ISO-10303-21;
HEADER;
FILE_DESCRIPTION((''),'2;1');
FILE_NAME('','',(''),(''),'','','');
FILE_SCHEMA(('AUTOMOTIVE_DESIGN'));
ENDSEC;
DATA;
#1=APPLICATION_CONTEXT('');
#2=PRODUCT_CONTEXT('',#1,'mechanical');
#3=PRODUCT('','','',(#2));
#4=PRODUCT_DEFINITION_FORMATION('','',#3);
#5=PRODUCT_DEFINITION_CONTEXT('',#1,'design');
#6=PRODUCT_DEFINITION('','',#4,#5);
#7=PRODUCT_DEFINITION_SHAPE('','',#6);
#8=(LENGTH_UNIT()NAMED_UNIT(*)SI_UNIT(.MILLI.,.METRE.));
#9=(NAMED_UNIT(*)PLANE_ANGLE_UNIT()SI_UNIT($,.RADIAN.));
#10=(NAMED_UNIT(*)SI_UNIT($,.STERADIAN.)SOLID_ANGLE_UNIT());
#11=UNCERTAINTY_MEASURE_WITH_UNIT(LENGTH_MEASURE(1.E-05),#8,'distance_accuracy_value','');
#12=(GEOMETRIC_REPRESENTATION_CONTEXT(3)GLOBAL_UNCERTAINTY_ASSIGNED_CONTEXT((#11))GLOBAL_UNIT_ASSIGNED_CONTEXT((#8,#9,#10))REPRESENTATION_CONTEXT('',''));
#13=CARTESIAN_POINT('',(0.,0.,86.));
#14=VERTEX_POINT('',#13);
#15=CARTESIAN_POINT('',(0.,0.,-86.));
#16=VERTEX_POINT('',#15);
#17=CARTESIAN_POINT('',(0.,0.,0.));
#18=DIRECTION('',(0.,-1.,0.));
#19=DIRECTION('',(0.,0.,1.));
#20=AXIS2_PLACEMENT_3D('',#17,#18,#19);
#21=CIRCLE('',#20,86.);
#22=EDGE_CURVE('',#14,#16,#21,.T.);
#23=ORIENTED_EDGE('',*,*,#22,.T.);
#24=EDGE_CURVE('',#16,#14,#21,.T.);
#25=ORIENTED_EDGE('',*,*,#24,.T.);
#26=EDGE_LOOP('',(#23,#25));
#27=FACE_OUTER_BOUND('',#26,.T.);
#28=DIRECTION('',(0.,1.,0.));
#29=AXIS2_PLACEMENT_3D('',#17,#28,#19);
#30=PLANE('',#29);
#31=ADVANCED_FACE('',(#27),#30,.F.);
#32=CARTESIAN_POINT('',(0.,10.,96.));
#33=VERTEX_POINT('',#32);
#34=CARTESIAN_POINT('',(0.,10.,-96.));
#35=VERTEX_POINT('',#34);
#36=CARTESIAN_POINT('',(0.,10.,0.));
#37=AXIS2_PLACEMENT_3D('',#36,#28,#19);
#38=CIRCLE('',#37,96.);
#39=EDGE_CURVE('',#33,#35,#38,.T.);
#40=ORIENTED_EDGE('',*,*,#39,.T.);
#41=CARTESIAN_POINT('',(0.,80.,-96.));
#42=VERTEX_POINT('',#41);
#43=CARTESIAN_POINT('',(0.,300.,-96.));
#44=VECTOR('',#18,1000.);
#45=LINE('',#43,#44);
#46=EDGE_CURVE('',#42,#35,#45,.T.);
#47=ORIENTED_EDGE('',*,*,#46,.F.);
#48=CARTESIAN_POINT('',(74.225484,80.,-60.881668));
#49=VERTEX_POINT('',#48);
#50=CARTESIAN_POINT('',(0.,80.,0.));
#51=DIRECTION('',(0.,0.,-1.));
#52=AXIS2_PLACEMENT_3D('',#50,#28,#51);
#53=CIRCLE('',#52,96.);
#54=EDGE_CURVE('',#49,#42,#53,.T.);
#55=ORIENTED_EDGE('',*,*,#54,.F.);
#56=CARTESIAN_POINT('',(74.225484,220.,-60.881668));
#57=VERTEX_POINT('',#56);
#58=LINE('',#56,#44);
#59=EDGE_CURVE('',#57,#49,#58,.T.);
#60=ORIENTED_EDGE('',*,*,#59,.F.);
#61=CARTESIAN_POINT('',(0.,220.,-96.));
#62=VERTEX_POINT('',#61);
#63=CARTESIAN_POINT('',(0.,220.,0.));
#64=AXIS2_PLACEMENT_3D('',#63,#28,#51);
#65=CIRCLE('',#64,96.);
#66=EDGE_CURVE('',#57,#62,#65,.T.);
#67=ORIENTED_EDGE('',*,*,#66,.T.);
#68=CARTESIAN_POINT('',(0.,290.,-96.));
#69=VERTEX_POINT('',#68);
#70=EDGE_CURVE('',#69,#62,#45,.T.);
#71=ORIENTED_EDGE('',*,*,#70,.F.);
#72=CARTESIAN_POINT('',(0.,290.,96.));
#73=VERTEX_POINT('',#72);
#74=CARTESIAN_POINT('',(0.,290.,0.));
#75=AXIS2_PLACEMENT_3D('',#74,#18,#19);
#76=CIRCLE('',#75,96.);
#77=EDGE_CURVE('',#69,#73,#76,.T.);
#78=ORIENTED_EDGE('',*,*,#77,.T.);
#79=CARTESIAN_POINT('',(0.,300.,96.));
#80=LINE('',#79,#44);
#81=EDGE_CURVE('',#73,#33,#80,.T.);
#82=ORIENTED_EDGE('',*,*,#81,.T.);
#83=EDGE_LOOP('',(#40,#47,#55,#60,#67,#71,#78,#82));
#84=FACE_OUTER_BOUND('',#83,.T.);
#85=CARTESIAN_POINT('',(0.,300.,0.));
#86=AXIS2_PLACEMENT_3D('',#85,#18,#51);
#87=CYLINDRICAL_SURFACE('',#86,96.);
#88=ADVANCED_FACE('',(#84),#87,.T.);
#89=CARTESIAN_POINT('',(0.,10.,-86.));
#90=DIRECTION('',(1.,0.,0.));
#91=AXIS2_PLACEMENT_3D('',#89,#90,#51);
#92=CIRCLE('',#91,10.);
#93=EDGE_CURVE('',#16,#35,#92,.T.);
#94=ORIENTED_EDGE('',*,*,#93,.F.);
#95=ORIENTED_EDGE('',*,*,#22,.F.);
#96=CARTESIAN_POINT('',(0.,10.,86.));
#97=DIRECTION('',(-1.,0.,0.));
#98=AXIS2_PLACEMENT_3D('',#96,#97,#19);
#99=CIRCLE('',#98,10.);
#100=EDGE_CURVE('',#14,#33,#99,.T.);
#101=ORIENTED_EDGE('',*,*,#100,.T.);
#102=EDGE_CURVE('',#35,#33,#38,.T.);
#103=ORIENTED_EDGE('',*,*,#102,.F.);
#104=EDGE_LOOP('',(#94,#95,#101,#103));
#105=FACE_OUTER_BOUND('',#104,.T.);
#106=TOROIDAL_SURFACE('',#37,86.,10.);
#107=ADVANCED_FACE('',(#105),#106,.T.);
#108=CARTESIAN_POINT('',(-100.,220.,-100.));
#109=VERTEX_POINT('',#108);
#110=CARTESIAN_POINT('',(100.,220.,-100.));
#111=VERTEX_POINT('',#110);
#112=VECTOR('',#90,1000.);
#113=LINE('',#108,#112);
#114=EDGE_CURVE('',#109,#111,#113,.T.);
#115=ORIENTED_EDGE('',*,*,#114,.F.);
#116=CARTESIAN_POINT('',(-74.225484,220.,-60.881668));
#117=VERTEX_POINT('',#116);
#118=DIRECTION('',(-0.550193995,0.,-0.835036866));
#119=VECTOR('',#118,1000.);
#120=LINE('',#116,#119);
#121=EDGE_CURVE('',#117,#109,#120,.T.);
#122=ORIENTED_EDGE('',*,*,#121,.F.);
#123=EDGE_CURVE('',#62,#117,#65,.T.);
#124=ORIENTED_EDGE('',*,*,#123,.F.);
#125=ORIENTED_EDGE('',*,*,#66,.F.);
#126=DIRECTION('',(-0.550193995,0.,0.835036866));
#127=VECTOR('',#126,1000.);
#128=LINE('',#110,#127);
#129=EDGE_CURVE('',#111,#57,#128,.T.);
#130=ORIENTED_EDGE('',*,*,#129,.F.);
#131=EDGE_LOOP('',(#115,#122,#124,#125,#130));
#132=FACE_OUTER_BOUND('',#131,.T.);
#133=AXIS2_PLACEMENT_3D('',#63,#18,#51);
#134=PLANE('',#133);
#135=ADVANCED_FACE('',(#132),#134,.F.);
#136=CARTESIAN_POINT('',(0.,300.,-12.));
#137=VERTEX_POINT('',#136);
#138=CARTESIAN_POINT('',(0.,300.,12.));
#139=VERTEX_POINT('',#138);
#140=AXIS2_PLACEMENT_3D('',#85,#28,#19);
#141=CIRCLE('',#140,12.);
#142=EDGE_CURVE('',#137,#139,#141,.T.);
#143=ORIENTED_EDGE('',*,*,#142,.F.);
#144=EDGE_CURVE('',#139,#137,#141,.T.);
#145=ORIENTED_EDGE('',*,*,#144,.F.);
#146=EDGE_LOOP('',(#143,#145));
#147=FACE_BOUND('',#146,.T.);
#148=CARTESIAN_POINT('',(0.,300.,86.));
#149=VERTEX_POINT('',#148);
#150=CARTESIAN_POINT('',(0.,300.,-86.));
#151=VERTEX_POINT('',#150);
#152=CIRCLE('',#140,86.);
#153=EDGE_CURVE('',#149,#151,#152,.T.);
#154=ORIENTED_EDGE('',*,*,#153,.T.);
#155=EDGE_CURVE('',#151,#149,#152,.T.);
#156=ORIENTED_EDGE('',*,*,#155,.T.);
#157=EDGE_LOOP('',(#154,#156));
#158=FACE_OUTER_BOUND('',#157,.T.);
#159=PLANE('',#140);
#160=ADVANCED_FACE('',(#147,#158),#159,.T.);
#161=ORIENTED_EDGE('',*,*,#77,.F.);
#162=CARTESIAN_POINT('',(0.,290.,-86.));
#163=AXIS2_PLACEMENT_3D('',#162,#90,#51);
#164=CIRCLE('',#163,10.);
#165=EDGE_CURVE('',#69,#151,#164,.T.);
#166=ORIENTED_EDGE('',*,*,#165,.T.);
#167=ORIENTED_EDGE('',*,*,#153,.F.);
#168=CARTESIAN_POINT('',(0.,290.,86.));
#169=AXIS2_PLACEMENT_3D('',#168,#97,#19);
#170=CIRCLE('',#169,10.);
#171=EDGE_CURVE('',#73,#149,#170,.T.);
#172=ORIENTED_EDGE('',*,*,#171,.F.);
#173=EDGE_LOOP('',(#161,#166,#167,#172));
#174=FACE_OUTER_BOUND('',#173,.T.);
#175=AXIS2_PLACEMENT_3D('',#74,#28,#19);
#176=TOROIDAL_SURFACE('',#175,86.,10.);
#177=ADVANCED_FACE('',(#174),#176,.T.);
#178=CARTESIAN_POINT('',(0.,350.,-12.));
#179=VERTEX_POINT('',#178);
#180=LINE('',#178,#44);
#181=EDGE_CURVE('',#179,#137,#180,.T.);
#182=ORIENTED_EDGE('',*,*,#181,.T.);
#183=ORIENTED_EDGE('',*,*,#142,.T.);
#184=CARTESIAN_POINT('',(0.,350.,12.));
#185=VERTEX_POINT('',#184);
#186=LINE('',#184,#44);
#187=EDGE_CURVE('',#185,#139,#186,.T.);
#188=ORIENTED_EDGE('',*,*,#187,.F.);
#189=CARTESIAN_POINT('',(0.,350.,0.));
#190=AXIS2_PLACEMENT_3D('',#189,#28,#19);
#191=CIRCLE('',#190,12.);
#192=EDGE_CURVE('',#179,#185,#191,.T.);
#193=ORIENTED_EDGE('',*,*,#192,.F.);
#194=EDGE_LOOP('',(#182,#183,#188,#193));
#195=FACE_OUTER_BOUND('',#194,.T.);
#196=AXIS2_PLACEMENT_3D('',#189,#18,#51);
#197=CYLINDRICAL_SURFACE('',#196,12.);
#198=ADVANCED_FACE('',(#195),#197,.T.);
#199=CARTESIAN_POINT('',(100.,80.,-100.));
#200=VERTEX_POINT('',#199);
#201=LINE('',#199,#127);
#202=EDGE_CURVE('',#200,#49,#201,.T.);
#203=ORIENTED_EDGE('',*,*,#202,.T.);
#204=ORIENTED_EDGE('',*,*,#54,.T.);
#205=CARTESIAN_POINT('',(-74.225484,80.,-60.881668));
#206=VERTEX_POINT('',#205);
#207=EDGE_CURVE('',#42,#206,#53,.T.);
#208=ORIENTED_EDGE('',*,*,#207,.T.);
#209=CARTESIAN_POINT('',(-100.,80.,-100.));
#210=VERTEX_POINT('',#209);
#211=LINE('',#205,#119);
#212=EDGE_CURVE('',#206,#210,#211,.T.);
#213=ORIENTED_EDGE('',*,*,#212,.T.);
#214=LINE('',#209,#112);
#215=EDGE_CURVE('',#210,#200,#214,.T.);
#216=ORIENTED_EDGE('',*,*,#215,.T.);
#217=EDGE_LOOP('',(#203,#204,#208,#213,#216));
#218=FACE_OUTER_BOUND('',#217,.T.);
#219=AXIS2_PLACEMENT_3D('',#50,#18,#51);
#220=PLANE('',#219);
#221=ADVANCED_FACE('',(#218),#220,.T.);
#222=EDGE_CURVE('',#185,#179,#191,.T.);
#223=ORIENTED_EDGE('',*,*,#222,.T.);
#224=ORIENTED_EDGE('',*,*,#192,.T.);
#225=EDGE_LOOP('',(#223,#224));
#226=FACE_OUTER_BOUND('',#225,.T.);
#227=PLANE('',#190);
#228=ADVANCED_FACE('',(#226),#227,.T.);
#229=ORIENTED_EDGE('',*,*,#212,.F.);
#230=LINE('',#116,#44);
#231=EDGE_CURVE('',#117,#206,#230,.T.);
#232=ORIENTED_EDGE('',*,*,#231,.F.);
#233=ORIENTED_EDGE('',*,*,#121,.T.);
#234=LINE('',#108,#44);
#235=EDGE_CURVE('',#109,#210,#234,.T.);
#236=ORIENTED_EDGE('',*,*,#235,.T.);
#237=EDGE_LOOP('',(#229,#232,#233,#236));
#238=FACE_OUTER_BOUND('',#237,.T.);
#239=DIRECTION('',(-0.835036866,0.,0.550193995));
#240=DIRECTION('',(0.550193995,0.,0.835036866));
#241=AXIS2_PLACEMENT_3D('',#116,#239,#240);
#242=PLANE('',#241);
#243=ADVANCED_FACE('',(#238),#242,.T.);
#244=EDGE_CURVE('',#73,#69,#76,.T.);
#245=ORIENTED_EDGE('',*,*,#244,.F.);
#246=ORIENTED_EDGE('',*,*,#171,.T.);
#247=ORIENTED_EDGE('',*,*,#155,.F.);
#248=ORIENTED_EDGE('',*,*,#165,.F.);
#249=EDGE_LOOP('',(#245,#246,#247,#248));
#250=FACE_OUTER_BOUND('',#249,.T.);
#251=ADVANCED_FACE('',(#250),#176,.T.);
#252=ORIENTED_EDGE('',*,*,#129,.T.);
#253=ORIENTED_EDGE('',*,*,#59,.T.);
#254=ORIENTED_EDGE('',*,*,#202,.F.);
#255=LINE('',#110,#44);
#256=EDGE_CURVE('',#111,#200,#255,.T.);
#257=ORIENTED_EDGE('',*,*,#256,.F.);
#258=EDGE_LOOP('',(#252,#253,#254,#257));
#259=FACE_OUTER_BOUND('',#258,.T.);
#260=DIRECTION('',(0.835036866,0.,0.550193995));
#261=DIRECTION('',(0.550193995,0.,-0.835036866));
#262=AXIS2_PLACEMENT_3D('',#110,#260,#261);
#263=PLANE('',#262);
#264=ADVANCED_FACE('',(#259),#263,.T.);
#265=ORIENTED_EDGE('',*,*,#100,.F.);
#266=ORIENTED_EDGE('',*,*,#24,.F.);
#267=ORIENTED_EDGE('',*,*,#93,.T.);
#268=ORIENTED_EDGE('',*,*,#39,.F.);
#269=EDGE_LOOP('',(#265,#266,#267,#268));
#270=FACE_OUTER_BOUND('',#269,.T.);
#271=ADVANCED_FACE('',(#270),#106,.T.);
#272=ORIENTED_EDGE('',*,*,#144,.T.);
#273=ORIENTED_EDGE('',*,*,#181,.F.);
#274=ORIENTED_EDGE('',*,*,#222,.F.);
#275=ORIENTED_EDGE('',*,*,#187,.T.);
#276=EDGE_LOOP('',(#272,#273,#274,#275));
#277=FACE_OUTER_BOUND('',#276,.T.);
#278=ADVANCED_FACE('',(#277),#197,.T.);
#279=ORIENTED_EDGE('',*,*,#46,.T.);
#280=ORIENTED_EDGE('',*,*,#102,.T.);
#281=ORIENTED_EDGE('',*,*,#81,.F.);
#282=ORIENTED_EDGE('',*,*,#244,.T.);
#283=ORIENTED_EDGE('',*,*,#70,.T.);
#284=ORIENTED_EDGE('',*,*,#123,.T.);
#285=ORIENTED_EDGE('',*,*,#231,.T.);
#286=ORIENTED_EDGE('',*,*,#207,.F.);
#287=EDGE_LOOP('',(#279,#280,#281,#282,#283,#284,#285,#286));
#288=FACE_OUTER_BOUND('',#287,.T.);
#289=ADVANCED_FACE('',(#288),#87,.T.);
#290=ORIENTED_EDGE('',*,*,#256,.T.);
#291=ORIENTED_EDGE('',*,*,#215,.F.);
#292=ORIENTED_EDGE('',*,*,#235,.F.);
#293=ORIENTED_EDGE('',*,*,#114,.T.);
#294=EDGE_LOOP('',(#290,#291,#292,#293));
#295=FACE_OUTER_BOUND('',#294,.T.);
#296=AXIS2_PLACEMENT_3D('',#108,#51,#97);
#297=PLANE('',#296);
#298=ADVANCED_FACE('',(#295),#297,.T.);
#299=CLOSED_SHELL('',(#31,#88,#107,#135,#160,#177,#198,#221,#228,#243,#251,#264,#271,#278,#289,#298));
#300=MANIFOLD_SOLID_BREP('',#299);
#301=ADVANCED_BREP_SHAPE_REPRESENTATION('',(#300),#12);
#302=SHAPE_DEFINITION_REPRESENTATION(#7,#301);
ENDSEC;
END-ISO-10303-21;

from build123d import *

# Parameters (mm, degrees)
SKETCH1_R           = 96
BOSS_EXTRUDE1_DEPTH = 300
SKETCH2_R           = 12
BOSS_EXTRUDE2_DEPTH = 50
FILLET1_R           = 10
BOSS_EXTRUDE3_DEPTH = 140


with BuildPart() as part:
    # Sketch1 → Boss-Extrude1 (new body)
    with BuildSketch(Plane(origin=(0, 0, 0), x_dir=(1, 0, 0), z_dir=(0, 1, 0))):
        with Locations(Location((0, 0, 0), (0, 0, 270))):
            Circle(SKETCH1_R)
    extrude(amount=BOSS_EXTRUDE1_DEPTH)

    # Sketch2 → Boss-Extrude2 (add)
    with BuildSketch(Plane(origin=(0, 300, 0), x_dir=(1, 0, 0), z_dir=(0, 1, 0))):
        with Locations(Location((0, 0, 0), (0, 0, 270))):
            Circle(SKETCH2_R)
    extrude(amount=BOSS_EXTRUDE2_DEPTH)

    # Fillet1
    fillet1_edges = [part.edges().sort_by_distance(p)[0] for p in [
        (0, 0, -96),
        (0, 300, -96),
    ]]
    fillet(fillet1_edges, radius=FILLET1_R)

    # Sketch3 → Boss-Extrude3 (add)
    with BuildSketch(Plane(origin=(0, 80, 0), x_dir=(-1, 0, 0), z_dir=(0, -1, 0))):
        with BuildLine():
            Line((74.225483886, 60.881668357), (100, 100))
            Line((100, 100), (-100, 100))
            Line((-100, 100), (-74.225483886, 60.881668357))
            ThreePointArc((-74.225483886, 60.881668357), (0, 96), (74.225483886, 60.881668357))
        make_face()
    extrude(amount=-BOSS_EXTRUDE3_DEPTH)


solid = part.part
